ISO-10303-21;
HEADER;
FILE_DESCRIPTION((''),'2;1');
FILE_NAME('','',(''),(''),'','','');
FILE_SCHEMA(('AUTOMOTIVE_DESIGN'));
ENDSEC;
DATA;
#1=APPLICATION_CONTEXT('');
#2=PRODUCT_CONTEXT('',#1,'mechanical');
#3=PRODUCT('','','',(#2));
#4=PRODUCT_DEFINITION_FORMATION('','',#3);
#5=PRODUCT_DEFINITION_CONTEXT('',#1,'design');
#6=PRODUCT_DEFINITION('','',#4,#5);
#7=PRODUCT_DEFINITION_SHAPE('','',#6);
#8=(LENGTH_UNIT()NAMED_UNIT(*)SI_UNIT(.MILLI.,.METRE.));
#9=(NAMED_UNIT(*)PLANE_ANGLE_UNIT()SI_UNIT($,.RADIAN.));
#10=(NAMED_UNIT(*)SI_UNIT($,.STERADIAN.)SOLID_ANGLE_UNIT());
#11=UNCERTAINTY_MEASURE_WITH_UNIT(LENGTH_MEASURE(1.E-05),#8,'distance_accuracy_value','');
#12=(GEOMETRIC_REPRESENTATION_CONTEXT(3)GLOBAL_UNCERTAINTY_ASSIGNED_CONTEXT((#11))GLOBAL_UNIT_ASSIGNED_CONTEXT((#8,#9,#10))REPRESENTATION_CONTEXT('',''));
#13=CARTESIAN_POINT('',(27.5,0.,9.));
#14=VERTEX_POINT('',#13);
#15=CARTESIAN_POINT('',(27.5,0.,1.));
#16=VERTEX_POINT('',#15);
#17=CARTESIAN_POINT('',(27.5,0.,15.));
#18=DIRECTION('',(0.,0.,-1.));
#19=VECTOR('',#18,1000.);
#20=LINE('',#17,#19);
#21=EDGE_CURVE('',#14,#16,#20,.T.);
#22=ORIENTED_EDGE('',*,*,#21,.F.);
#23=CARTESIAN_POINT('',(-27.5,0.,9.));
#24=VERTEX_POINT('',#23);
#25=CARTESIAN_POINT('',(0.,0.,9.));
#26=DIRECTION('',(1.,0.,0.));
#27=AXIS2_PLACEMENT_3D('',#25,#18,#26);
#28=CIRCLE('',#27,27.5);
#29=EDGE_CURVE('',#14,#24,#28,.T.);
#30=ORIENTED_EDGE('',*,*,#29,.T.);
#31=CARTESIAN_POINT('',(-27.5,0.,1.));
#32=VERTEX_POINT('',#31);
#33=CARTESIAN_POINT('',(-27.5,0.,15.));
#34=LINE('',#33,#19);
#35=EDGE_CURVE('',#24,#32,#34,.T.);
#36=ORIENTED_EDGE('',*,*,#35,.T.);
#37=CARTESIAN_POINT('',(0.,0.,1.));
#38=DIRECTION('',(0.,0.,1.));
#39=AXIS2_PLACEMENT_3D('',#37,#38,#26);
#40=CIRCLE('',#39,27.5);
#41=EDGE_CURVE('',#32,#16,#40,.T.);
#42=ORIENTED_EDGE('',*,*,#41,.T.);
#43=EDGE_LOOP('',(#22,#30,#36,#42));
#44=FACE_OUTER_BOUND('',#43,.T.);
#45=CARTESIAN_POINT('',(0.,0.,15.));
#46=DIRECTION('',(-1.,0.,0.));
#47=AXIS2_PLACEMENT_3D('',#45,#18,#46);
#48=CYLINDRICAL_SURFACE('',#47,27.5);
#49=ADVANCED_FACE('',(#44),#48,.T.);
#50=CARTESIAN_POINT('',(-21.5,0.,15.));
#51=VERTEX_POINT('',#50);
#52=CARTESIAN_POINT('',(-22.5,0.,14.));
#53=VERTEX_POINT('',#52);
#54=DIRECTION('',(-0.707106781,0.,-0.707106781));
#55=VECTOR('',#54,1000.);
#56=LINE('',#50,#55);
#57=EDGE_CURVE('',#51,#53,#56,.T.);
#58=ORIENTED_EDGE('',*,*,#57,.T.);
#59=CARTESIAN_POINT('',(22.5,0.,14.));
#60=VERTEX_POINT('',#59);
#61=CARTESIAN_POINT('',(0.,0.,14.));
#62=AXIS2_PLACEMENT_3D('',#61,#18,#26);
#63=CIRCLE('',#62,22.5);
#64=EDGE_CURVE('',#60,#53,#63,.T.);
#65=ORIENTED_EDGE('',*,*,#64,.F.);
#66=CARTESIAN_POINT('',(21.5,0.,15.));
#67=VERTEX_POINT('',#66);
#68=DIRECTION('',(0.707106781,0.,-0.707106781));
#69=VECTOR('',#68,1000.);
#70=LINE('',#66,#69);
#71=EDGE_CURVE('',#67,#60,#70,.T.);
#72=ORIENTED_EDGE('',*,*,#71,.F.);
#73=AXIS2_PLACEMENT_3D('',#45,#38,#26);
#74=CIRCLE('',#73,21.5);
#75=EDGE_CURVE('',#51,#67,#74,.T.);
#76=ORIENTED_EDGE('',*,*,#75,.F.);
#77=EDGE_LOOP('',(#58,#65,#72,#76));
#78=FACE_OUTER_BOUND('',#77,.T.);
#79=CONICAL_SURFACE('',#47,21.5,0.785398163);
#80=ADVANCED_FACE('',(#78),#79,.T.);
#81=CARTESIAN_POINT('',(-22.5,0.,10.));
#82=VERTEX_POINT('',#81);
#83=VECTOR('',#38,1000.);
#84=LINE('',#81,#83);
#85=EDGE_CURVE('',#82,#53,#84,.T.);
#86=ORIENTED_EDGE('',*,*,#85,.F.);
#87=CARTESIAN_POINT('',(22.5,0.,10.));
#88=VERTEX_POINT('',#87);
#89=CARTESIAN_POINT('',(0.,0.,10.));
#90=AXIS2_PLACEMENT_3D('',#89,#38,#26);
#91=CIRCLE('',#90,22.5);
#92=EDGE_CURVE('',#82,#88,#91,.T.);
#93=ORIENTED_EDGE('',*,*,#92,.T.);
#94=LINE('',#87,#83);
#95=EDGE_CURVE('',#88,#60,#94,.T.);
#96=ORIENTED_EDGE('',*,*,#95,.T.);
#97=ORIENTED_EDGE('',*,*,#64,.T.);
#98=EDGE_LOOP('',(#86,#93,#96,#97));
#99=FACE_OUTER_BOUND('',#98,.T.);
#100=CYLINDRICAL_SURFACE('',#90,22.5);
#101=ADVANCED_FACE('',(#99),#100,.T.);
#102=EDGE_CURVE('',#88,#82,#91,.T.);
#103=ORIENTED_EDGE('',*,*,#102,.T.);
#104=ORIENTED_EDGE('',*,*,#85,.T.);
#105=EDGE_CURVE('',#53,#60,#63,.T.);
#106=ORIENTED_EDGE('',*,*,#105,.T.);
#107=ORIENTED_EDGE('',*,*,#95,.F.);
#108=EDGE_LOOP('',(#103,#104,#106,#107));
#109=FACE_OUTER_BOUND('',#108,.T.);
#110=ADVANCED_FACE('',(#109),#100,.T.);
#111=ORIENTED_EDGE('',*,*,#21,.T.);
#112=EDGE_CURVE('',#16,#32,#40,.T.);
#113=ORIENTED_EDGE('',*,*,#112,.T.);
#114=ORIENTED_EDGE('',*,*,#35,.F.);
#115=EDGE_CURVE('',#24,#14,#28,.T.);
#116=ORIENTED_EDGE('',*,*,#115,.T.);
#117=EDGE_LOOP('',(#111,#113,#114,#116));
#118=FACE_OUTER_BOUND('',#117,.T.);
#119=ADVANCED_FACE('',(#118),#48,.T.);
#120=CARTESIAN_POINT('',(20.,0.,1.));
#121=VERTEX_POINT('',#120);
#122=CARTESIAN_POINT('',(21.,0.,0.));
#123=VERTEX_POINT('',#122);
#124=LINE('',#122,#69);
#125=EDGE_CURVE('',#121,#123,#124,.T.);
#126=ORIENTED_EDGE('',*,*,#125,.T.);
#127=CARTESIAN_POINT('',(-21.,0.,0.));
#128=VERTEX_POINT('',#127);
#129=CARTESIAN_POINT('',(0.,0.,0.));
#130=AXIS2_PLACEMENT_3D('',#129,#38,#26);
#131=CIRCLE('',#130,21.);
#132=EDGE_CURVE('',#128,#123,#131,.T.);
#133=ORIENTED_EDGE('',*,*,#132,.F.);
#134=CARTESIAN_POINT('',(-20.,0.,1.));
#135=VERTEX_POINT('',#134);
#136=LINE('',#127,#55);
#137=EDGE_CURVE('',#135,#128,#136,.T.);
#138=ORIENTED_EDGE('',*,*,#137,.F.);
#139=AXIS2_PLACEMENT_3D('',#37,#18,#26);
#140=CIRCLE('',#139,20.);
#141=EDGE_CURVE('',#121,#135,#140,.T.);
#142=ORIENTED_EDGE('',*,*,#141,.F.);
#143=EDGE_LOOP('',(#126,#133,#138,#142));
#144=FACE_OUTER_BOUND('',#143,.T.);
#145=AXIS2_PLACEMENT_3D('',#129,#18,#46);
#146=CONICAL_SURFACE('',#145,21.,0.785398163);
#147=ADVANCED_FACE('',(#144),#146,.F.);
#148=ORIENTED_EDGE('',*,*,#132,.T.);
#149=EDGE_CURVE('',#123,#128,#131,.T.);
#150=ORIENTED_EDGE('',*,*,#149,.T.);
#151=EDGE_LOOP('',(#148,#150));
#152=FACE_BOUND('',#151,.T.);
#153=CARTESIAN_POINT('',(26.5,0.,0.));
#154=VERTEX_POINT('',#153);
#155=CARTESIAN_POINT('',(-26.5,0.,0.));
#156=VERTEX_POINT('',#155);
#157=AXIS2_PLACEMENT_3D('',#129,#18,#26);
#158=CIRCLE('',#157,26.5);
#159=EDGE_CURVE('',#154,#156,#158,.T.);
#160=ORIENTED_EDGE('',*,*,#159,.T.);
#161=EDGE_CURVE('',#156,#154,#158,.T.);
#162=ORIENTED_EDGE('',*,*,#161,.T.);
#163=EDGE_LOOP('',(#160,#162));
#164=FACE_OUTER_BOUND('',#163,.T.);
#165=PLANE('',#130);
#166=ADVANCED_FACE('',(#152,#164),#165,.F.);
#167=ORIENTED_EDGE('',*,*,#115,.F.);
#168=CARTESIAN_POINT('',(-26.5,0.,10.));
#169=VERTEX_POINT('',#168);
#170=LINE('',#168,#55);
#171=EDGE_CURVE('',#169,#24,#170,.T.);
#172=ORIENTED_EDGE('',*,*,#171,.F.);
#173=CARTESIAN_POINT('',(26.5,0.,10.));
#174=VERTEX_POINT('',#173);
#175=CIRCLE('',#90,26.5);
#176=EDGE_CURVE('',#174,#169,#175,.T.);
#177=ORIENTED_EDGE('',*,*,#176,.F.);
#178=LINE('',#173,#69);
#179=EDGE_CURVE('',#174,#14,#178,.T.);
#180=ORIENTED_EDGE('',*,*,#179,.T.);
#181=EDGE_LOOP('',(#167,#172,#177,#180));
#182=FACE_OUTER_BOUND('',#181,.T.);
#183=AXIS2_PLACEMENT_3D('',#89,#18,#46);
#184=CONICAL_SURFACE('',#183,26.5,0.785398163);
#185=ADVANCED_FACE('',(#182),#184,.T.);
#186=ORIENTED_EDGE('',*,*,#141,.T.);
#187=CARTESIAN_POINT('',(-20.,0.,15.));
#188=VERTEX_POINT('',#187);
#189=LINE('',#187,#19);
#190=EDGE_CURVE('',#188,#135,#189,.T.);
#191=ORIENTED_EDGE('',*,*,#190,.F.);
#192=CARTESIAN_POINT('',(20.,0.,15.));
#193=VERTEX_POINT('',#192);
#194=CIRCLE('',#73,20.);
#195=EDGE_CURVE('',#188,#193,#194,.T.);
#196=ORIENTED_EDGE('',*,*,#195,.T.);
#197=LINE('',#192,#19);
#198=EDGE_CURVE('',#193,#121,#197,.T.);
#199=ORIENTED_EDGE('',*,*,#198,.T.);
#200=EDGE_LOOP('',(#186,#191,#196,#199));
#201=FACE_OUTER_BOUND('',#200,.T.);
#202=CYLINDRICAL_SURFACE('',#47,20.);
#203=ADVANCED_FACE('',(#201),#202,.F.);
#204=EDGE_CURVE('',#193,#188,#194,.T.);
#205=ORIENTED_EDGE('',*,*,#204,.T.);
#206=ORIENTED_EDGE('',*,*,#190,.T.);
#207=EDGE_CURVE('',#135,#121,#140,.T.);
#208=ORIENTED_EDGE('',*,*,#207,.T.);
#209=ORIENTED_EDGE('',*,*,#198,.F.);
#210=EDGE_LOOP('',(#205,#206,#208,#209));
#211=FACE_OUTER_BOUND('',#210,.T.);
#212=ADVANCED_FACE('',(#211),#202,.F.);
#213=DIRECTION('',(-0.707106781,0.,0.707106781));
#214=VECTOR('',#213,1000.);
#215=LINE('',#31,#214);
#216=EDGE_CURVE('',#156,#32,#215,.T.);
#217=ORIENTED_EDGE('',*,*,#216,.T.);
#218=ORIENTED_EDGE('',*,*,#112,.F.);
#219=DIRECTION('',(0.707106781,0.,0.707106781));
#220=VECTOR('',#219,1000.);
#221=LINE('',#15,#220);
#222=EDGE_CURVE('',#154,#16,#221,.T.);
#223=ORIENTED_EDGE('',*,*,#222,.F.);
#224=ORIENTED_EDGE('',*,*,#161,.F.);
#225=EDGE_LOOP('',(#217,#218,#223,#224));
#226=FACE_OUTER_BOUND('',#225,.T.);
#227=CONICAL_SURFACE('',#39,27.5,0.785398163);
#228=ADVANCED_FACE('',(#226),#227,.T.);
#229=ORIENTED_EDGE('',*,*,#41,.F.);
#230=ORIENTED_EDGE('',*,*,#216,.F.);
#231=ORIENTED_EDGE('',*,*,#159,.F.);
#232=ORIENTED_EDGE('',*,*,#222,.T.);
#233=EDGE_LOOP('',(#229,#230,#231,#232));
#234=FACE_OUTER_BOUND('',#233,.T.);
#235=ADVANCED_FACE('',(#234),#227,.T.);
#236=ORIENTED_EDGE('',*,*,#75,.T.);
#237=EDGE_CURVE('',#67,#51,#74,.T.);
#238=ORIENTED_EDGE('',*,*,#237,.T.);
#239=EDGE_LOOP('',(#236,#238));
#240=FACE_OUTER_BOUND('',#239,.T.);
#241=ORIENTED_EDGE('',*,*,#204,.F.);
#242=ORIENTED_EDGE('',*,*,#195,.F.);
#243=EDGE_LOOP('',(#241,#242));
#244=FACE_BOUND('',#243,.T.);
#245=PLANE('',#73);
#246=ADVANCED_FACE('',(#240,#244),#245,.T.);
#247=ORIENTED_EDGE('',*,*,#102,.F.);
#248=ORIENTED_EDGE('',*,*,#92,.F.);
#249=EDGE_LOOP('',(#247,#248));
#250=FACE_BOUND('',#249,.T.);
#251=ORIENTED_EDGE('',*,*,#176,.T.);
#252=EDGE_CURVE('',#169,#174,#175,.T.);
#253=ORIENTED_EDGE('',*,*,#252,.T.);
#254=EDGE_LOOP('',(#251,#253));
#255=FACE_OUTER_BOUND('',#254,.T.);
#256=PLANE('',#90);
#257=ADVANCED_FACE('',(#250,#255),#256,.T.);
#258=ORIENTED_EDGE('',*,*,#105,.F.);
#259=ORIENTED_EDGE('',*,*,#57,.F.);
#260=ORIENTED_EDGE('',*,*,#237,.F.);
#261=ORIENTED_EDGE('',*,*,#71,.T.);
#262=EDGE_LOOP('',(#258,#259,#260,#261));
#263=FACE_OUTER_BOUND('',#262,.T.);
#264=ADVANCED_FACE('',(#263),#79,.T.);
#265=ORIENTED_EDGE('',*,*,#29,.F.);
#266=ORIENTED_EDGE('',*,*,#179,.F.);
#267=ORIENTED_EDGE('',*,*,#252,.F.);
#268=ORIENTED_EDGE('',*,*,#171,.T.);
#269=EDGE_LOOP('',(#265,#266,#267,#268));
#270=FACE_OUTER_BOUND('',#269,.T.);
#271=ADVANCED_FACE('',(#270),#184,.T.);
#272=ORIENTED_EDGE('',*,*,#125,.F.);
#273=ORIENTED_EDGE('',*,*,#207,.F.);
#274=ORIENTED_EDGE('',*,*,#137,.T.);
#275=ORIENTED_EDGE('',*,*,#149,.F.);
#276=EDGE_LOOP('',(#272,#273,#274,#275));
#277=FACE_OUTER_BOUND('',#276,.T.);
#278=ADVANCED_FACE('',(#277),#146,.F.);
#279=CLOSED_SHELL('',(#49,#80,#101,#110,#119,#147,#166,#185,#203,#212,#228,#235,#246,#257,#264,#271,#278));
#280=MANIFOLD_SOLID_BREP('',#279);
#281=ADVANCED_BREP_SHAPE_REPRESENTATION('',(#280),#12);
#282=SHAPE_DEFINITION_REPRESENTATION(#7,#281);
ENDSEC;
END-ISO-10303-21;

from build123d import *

# Parameters (mm, degrees)
SKETCH1_R           = 27.5
SKETCH1_R_2         = 20
BOSS_EXTRUDE1_DEPTH = 15
CUT_EXTRUDE1_START  = -5
SKETCH2_R           = 27.5
SKETCH2_R_2         = 22.5
CUT_EXTRUDE1_DEPTH  = 5
CHAMFER1_SIZE       = 1


with BuildPart() as part:
    # Sketch1 → Boss-Extrude1 (new body)
    with BuildSketch(Plane.XY):
        Circle(SKETCH1_R)
        Circle(SKETCH1_R_2, mode=Mode.SUBTRACT)
    extrude(amount=BOSS_EXTRUDE1_DEPTH)

    # Sketch2 → Cut-Extrude1 (cut)
    with BuildSketch(Plane.XY.offset(15).offset(CUT_EXTRUDE1_START)):
        Circle(SKETCH2_R)
        Circle(SKETCH2_R_2, mode=Mode.SUBTRACT)
    extrude(amount=CUT_EXTRUDE1_DEPTH, mode=Mode.SUBTRACT)

    # Chamfer1
    chamfer1_edges = [part.edges().sort_by_distance(p)[0] for p in [
        (-27.5, 0, 10),
        (-22.5, 0, 15),
        (-27.5, 0, 0),
        (-20, 0, 0),
    ]]
    chamfer(chamfer1_edges, length=CHAMFER1_SIZE)


solid = part.part
